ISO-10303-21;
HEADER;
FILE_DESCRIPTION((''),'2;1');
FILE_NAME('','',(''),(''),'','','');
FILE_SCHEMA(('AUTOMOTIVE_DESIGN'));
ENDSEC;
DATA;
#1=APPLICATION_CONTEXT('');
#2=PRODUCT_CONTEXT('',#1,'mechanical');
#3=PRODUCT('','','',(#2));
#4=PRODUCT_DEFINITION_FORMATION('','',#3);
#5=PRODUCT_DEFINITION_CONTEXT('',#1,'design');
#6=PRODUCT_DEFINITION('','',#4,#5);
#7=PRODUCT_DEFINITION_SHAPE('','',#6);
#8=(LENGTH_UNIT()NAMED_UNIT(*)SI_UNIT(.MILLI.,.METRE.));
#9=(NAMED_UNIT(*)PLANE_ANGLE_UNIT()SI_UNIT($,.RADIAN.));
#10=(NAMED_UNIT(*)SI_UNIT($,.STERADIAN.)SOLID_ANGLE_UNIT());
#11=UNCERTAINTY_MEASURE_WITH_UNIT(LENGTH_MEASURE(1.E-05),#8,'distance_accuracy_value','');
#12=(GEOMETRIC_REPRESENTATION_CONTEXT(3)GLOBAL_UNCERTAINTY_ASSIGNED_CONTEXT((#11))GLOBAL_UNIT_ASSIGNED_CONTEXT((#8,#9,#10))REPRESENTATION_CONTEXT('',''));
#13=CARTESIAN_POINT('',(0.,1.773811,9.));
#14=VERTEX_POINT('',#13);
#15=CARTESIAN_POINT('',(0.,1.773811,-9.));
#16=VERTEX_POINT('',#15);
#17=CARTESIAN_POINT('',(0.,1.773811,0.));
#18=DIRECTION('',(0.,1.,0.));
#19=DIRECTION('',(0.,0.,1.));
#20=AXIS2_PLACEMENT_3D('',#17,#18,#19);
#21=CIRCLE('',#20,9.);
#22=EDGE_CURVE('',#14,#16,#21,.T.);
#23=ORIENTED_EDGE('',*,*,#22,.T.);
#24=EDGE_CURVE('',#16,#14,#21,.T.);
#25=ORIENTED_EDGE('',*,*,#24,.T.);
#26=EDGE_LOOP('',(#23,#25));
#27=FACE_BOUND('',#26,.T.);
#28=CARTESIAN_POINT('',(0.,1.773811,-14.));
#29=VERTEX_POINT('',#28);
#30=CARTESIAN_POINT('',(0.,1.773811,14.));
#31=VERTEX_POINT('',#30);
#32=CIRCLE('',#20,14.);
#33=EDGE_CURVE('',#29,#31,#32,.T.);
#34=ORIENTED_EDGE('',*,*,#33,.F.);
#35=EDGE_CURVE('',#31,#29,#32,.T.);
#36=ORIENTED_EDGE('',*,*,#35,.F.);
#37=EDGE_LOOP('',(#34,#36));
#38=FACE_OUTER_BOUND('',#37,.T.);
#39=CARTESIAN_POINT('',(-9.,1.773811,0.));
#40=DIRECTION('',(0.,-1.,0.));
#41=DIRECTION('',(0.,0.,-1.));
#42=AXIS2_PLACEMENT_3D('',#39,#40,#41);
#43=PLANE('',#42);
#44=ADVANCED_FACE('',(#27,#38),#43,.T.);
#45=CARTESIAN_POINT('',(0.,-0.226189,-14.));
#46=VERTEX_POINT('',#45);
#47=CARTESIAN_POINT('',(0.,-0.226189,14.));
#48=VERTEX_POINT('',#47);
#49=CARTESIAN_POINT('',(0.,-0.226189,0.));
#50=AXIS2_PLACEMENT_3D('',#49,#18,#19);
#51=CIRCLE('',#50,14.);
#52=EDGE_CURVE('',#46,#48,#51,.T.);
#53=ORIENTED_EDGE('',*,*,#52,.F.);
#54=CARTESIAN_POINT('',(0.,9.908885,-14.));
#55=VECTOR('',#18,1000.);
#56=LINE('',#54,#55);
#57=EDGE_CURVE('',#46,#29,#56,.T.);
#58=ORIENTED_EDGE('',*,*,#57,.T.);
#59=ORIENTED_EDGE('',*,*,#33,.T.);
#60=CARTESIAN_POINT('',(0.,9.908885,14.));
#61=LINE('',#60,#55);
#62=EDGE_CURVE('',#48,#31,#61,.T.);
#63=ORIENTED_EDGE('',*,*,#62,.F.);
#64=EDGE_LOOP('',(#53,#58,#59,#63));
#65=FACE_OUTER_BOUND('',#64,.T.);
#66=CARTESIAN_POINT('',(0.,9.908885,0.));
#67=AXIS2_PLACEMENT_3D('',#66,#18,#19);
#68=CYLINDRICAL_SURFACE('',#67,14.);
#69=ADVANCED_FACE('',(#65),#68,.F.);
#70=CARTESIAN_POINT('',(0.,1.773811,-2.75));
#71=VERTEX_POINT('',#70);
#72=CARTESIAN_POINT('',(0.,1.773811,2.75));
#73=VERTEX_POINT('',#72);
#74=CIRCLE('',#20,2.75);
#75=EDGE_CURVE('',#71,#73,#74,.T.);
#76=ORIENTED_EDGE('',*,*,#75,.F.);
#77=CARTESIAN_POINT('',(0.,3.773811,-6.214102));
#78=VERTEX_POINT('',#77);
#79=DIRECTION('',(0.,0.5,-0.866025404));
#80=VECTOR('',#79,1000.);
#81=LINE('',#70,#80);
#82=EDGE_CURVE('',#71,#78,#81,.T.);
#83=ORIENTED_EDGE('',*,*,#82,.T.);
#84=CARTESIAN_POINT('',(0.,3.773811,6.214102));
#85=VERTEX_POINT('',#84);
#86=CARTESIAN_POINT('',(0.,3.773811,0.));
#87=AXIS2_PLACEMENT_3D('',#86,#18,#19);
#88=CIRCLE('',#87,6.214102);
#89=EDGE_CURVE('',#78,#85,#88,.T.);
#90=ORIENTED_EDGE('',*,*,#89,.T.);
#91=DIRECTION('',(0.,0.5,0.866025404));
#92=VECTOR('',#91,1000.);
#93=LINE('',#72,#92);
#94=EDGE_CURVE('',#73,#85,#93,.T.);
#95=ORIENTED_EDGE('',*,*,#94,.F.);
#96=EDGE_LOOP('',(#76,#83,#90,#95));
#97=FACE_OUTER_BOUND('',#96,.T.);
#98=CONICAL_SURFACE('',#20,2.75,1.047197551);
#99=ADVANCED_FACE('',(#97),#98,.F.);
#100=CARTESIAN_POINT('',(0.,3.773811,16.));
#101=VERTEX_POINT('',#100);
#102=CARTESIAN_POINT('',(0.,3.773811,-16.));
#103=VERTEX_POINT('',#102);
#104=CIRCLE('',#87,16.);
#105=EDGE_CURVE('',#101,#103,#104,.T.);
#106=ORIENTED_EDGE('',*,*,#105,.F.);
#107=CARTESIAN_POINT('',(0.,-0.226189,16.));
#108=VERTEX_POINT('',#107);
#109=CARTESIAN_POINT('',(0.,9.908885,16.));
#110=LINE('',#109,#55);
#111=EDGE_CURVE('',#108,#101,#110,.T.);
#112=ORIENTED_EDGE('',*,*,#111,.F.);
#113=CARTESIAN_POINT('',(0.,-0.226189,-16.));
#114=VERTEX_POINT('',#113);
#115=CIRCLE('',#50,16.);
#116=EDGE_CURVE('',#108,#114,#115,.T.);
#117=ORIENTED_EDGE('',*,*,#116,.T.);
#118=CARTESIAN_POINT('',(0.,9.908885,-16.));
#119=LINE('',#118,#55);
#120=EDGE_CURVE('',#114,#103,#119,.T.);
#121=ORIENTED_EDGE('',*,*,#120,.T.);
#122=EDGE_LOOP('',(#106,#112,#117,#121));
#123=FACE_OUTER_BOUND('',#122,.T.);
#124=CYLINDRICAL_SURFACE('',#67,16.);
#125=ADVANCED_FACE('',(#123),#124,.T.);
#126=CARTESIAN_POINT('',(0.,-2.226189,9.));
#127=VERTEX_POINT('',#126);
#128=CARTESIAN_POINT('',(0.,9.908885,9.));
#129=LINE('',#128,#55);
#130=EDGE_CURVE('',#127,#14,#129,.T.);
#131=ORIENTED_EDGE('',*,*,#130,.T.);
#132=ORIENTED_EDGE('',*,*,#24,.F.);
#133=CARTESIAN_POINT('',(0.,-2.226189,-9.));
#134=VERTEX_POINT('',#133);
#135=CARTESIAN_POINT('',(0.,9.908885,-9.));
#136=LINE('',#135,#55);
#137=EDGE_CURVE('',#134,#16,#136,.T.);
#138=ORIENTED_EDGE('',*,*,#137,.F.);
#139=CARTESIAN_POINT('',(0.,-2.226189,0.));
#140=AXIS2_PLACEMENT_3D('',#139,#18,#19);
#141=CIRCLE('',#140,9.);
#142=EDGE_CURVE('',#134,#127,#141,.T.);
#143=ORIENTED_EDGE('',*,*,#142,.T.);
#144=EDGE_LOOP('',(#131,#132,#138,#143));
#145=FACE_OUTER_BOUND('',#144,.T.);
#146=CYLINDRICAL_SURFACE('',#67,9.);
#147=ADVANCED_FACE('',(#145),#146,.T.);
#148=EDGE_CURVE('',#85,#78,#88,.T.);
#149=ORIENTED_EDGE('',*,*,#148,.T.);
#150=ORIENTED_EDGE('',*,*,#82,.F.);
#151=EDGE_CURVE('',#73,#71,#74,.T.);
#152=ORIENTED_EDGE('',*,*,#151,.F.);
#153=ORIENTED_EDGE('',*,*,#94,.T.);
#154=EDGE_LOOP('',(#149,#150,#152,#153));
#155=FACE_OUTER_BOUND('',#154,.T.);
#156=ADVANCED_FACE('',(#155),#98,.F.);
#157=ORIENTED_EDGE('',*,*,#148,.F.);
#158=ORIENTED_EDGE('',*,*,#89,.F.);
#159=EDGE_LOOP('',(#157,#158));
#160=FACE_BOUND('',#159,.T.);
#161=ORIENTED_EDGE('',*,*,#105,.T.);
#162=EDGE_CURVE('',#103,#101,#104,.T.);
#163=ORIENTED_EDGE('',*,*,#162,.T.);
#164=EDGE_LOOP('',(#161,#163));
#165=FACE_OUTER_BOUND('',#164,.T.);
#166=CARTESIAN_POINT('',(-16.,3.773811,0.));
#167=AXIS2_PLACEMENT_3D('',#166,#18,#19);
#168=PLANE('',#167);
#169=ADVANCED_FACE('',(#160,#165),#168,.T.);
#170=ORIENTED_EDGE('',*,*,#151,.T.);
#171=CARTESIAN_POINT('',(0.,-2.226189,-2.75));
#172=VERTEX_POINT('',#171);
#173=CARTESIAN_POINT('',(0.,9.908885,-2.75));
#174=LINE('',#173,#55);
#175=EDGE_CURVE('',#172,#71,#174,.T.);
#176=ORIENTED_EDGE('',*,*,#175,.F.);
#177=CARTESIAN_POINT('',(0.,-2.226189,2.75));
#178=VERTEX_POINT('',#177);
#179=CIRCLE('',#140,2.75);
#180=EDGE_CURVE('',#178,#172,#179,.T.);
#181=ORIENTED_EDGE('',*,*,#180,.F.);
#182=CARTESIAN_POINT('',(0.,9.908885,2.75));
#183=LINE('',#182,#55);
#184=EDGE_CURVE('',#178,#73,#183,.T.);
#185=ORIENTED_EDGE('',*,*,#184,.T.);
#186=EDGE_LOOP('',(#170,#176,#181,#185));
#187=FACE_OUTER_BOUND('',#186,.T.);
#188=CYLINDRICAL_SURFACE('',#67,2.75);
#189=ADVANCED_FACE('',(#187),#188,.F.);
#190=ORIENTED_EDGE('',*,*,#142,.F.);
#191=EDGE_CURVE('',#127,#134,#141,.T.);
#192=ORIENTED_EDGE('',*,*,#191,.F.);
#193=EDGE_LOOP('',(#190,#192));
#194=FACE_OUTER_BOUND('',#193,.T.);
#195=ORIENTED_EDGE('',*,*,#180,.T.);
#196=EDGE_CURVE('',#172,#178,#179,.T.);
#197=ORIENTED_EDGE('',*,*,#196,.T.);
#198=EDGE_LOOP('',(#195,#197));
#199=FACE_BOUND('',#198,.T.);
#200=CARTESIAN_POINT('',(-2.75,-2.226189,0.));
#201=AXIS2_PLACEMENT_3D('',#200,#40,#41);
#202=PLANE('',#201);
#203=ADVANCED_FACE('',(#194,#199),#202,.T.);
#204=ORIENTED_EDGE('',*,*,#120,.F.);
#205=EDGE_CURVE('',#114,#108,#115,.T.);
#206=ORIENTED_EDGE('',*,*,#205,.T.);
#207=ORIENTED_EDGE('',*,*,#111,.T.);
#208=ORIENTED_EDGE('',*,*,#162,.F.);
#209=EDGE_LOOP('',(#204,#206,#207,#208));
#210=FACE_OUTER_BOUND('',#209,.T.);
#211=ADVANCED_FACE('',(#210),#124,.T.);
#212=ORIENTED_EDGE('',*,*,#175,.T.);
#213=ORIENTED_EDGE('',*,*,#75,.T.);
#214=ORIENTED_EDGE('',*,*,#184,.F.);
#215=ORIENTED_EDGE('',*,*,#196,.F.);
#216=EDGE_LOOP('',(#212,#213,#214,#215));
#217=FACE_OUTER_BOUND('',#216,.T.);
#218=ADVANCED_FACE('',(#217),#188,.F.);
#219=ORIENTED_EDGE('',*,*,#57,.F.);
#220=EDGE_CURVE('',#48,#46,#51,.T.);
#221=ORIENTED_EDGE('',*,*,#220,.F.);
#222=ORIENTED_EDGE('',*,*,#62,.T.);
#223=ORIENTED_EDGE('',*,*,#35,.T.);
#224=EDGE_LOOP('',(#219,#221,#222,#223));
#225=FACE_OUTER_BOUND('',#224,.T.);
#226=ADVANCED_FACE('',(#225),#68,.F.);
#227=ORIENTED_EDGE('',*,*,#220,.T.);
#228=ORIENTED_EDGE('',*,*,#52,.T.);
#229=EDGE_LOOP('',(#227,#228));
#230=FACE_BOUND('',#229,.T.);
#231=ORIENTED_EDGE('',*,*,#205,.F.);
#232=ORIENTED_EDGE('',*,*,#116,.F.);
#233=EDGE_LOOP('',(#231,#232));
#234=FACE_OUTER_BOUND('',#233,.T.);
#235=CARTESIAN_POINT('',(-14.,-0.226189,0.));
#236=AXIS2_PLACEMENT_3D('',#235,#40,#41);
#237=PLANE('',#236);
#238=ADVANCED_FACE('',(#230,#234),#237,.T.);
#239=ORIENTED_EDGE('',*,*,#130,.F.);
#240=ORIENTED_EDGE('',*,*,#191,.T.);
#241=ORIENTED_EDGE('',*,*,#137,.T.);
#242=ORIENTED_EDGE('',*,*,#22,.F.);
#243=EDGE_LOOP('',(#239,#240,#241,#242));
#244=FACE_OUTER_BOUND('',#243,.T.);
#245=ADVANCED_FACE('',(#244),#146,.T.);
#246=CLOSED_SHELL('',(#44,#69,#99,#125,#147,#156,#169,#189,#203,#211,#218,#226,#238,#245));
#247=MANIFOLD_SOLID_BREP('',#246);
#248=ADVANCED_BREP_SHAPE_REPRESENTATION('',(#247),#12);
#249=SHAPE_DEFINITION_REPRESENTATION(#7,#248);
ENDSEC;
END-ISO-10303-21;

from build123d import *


with BuildPart() as part:
    # Sketch1 → Revolve1 (revolve)
    with BuildSketch(Plane.XY, mode=Mode.PRIVATE) as revolve1_sk:
        Polygon((-2.75, -2.226189364), (-9, -2.226189364), (-9, 1.773810636), (-14, 1.773810636), (-14, -0.226189364), (-16, -0.226189364), (-16, 3.773810636), (-6.214101615, 3.773810636), (-2.75, 1.773810636), align=None)
    revolve(revolve1_sk.sketch.rotate(Axis((0, 9.90888507, 0), (0, -1, 0)), 270), axis=Axis((0, 9.90888507, 0), (0, -1, 0)))


solid = part.part
